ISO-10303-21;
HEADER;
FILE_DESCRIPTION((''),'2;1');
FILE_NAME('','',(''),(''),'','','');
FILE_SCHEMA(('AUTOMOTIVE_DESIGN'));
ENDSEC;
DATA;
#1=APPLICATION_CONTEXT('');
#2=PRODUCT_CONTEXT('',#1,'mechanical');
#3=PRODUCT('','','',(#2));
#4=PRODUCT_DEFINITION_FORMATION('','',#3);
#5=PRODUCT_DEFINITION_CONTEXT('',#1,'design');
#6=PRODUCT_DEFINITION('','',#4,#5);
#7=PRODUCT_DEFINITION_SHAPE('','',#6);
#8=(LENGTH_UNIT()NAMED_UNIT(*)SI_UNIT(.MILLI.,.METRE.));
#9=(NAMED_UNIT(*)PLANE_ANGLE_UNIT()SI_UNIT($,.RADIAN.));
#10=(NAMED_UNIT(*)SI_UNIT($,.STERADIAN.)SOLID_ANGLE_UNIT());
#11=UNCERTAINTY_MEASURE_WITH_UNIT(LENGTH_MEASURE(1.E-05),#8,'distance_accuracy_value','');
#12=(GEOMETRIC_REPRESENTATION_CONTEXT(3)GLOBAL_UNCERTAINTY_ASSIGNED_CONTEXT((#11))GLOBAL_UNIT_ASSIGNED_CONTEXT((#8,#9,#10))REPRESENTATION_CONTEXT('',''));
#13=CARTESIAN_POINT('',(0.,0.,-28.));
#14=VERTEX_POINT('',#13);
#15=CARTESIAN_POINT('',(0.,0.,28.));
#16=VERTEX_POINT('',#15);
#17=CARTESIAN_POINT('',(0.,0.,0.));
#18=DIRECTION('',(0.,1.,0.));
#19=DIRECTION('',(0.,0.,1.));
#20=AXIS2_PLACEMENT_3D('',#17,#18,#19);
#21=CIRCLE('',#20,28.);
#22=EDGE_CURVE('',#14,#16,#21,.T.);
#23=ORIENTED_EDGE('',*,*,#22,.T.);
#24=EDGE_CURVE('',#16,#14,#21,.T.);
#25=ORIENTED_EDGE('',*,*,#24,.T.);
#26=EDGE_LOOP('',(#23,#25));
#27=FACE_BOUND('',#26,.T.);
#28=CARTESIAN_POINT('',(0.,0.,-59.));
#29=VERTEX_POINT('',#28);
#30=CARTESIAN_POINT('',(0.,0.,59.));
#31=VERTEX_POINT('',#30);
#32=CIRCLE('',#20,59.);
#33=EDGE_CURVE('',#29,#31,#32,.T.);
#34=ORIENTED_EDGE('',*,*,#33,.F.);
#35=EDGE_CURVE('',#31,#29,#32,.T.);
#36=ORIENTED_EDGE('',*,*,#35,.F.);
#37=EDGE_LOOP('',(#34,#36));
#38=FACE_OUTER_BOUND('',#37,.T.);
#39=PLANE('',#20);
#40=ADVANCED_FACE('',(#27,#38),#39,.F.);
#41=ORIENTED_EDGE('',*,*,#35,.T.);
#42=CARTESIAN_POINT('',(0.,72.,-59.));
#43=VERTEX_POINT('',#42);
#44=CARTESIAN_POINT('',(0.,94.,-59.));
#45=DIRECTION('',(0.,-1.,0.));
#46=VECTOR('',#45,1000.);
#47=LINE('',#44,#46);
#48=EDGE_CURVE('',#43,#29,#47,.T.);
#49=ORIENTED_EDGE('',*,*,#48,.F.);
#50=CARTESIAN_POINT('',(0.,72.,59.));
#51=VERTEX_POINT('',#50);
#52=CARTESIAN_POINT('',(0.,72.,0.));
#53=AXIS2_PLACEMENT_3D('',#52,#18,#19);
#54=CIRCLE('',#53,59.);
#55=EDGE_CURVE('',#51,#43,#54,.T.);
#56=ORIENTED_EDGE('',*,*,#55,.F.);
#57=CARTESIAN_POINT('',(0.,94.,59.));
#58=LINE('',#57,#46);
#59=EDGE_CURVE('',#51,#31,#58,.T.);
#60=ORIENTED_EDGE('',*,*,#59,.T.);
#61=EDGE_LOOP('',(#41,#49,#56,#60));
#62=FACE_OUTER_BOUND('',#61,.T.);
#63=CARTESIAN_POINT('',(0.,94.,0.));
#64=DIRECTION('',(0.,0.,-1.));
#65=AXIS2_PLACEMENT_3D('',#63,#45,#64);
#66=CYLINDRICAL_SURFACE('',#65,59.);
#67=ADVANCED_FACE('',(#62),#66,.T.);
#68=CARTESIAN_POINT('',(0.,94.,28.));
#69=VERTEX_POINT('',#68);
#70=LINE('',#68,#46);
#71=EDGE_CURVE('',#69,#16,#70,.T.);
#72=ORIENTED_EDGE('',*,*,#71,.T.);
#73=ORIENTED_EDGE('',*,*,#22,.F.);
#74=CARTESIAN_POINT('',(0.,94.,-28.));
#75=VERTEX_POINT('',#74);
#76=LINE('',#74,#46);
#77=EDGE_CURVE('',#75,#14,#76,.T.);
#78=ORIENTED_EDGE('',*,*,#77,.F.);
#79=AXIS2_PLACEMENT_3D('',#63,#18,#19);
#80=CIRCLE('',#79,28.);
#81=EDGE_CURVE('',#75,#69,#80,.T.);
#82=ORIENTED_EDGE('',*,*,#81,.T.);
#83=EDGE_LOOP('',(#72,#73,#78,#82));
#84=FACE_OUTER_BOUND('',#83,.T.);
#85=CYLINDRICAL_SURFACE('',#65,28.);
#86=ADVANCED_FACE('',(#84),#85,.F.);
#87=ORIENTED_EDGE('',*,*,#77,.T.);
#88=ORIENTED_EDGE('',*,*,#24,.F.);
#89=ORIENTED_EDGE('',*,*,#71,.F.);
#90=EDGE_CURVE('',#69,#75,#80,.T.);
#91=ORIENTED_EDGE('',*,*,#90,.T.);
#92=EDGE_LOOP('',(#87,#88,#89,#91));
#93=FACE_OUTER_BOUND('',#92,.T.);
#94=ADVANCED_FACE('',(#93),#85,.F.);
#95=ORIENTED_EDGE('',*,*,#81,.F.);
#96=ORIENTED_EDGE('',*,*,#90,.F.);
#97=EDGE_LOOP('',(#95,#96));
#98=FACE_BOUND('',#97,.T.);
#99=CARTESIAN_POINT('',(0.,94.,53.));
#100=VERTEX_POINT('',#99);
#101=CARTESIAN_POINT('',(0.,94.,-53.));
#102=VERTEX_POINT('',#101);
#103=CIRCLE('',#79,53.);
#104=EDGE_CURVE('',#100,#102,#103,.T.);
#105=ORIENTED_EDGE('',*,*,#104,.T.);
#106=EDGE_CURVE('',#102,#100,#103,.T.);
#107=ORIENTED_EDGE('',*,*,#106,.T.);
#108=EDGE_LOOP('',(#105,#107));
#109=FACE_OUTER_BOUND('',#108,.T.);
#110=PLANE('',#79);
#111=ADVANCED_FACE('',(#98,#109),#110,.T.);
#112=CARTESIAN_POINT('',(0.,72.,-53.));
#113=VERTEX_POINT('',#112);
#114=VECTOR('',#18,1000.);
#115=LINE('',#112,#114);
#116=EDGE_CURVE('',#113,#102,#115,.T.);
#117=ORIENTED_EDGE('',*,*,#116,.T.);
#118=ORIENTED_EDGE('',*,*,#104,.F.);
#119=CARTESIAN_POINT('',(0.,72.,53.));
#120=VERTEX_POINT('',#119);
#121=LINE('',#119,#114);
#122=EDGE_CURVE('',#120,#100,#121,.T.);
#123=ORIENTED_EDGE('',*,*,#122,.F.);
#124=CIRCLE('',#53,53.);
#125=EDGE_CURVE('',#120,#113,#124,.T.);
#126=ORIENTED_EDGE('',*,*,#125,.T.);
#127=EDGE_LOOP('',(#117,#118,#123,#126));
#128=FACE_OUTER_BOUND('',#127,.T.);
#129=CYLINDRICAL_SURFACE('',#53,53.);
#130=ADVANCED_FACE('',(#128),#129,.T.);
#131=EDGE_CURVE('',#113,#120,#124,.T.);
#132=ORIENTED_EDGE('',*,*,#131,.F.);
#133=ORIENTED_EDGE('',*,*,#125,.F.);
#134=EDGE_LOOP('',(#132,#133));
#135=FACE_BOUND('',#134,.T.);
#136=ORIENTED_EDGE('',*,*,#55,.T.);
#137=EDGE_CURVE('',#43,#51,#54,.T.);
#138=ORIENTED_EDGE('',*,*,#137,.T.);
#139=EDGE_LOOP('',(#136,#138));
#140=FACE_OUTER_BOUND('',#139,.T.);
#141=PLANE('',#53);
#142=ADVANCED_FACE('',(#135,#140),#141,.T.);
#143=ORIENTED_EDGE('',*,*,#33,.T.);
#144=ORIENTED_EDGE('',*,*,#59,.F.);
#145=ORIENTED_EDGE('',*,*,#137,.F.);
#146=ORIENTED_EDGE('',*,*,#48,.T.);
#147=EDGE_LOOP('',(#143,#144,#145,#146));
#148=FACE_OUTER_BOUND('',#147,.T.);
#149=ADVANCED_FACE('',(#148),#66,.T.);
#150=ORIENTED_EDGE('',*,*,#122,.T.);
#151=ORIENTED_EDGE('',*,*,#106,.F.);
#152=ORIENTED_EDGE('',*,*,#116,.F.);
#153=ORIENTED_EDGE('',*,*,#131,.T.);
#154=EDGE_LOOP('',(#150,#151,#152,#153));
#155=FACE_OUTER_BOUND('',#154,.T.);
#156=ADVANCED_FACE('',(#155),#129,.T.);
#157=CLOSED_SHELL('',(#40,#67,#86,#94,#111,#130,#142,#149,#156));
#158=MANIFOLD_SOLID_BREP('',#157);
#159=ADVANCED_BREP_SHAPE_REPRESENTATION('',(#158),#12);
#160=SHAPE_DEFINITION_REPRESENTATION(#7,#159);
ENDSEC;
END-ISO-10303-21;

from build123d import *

# Parameters (mm, degrees)
SKETCH_1_R          = 59
SKETCH_1_R_2        = 28
EXTRUDE_1_DEPTH     = 94
SKETCH_2_OUTSIDE_W  = 158.306
SKETCH_2_OUTSIDE_H  = 158.306
SKETCH_2_OUTSIDE_R  = 53
CUT_EXTRUDE_1_DEPTH = 22


with BuildPart() as part:
    # 草图1 → 凸台-拉伸1 (new body)
    with BuildSketch(Plane(origin=(0, 0, 0), x_dir=(1, 0, 0), z_dir=(0, 1, 0))):
        with Locations(Location((0, 0, 0), (0, 0, 270))):
            Circle(SKETCH_1_R)
        with Locations(Location((0, 0, 0), (0, 0, 270))):
            Circle(SKETCH_1_R_2, mode=Mode.SUBTRACT)
    extrude(amount=EXTRUDE_1_DEPTH)

    # 草图2 outside → 切除-拉伸1 (cut)
    with BuildSketch(Plane(origin=(0, 94, 0), x_dir=(1, 0, 0), z_dir=(0, 1, 0))):
        Rectangle(SKETCH_2_OUTSIDE_W, SKETCH_2_OUTSIDE_H)
        with Locations(Location((0, 0, 0), (0, 0, 270))):
            Circle(SKETCH_2_OUTSIDE_R, mode=Mode.SUBTRACT)
    extrude(amount=-CUT_EXTRUDE_1_DEPTH, mode=Mode.SUBTRACT)


solid = part.part
